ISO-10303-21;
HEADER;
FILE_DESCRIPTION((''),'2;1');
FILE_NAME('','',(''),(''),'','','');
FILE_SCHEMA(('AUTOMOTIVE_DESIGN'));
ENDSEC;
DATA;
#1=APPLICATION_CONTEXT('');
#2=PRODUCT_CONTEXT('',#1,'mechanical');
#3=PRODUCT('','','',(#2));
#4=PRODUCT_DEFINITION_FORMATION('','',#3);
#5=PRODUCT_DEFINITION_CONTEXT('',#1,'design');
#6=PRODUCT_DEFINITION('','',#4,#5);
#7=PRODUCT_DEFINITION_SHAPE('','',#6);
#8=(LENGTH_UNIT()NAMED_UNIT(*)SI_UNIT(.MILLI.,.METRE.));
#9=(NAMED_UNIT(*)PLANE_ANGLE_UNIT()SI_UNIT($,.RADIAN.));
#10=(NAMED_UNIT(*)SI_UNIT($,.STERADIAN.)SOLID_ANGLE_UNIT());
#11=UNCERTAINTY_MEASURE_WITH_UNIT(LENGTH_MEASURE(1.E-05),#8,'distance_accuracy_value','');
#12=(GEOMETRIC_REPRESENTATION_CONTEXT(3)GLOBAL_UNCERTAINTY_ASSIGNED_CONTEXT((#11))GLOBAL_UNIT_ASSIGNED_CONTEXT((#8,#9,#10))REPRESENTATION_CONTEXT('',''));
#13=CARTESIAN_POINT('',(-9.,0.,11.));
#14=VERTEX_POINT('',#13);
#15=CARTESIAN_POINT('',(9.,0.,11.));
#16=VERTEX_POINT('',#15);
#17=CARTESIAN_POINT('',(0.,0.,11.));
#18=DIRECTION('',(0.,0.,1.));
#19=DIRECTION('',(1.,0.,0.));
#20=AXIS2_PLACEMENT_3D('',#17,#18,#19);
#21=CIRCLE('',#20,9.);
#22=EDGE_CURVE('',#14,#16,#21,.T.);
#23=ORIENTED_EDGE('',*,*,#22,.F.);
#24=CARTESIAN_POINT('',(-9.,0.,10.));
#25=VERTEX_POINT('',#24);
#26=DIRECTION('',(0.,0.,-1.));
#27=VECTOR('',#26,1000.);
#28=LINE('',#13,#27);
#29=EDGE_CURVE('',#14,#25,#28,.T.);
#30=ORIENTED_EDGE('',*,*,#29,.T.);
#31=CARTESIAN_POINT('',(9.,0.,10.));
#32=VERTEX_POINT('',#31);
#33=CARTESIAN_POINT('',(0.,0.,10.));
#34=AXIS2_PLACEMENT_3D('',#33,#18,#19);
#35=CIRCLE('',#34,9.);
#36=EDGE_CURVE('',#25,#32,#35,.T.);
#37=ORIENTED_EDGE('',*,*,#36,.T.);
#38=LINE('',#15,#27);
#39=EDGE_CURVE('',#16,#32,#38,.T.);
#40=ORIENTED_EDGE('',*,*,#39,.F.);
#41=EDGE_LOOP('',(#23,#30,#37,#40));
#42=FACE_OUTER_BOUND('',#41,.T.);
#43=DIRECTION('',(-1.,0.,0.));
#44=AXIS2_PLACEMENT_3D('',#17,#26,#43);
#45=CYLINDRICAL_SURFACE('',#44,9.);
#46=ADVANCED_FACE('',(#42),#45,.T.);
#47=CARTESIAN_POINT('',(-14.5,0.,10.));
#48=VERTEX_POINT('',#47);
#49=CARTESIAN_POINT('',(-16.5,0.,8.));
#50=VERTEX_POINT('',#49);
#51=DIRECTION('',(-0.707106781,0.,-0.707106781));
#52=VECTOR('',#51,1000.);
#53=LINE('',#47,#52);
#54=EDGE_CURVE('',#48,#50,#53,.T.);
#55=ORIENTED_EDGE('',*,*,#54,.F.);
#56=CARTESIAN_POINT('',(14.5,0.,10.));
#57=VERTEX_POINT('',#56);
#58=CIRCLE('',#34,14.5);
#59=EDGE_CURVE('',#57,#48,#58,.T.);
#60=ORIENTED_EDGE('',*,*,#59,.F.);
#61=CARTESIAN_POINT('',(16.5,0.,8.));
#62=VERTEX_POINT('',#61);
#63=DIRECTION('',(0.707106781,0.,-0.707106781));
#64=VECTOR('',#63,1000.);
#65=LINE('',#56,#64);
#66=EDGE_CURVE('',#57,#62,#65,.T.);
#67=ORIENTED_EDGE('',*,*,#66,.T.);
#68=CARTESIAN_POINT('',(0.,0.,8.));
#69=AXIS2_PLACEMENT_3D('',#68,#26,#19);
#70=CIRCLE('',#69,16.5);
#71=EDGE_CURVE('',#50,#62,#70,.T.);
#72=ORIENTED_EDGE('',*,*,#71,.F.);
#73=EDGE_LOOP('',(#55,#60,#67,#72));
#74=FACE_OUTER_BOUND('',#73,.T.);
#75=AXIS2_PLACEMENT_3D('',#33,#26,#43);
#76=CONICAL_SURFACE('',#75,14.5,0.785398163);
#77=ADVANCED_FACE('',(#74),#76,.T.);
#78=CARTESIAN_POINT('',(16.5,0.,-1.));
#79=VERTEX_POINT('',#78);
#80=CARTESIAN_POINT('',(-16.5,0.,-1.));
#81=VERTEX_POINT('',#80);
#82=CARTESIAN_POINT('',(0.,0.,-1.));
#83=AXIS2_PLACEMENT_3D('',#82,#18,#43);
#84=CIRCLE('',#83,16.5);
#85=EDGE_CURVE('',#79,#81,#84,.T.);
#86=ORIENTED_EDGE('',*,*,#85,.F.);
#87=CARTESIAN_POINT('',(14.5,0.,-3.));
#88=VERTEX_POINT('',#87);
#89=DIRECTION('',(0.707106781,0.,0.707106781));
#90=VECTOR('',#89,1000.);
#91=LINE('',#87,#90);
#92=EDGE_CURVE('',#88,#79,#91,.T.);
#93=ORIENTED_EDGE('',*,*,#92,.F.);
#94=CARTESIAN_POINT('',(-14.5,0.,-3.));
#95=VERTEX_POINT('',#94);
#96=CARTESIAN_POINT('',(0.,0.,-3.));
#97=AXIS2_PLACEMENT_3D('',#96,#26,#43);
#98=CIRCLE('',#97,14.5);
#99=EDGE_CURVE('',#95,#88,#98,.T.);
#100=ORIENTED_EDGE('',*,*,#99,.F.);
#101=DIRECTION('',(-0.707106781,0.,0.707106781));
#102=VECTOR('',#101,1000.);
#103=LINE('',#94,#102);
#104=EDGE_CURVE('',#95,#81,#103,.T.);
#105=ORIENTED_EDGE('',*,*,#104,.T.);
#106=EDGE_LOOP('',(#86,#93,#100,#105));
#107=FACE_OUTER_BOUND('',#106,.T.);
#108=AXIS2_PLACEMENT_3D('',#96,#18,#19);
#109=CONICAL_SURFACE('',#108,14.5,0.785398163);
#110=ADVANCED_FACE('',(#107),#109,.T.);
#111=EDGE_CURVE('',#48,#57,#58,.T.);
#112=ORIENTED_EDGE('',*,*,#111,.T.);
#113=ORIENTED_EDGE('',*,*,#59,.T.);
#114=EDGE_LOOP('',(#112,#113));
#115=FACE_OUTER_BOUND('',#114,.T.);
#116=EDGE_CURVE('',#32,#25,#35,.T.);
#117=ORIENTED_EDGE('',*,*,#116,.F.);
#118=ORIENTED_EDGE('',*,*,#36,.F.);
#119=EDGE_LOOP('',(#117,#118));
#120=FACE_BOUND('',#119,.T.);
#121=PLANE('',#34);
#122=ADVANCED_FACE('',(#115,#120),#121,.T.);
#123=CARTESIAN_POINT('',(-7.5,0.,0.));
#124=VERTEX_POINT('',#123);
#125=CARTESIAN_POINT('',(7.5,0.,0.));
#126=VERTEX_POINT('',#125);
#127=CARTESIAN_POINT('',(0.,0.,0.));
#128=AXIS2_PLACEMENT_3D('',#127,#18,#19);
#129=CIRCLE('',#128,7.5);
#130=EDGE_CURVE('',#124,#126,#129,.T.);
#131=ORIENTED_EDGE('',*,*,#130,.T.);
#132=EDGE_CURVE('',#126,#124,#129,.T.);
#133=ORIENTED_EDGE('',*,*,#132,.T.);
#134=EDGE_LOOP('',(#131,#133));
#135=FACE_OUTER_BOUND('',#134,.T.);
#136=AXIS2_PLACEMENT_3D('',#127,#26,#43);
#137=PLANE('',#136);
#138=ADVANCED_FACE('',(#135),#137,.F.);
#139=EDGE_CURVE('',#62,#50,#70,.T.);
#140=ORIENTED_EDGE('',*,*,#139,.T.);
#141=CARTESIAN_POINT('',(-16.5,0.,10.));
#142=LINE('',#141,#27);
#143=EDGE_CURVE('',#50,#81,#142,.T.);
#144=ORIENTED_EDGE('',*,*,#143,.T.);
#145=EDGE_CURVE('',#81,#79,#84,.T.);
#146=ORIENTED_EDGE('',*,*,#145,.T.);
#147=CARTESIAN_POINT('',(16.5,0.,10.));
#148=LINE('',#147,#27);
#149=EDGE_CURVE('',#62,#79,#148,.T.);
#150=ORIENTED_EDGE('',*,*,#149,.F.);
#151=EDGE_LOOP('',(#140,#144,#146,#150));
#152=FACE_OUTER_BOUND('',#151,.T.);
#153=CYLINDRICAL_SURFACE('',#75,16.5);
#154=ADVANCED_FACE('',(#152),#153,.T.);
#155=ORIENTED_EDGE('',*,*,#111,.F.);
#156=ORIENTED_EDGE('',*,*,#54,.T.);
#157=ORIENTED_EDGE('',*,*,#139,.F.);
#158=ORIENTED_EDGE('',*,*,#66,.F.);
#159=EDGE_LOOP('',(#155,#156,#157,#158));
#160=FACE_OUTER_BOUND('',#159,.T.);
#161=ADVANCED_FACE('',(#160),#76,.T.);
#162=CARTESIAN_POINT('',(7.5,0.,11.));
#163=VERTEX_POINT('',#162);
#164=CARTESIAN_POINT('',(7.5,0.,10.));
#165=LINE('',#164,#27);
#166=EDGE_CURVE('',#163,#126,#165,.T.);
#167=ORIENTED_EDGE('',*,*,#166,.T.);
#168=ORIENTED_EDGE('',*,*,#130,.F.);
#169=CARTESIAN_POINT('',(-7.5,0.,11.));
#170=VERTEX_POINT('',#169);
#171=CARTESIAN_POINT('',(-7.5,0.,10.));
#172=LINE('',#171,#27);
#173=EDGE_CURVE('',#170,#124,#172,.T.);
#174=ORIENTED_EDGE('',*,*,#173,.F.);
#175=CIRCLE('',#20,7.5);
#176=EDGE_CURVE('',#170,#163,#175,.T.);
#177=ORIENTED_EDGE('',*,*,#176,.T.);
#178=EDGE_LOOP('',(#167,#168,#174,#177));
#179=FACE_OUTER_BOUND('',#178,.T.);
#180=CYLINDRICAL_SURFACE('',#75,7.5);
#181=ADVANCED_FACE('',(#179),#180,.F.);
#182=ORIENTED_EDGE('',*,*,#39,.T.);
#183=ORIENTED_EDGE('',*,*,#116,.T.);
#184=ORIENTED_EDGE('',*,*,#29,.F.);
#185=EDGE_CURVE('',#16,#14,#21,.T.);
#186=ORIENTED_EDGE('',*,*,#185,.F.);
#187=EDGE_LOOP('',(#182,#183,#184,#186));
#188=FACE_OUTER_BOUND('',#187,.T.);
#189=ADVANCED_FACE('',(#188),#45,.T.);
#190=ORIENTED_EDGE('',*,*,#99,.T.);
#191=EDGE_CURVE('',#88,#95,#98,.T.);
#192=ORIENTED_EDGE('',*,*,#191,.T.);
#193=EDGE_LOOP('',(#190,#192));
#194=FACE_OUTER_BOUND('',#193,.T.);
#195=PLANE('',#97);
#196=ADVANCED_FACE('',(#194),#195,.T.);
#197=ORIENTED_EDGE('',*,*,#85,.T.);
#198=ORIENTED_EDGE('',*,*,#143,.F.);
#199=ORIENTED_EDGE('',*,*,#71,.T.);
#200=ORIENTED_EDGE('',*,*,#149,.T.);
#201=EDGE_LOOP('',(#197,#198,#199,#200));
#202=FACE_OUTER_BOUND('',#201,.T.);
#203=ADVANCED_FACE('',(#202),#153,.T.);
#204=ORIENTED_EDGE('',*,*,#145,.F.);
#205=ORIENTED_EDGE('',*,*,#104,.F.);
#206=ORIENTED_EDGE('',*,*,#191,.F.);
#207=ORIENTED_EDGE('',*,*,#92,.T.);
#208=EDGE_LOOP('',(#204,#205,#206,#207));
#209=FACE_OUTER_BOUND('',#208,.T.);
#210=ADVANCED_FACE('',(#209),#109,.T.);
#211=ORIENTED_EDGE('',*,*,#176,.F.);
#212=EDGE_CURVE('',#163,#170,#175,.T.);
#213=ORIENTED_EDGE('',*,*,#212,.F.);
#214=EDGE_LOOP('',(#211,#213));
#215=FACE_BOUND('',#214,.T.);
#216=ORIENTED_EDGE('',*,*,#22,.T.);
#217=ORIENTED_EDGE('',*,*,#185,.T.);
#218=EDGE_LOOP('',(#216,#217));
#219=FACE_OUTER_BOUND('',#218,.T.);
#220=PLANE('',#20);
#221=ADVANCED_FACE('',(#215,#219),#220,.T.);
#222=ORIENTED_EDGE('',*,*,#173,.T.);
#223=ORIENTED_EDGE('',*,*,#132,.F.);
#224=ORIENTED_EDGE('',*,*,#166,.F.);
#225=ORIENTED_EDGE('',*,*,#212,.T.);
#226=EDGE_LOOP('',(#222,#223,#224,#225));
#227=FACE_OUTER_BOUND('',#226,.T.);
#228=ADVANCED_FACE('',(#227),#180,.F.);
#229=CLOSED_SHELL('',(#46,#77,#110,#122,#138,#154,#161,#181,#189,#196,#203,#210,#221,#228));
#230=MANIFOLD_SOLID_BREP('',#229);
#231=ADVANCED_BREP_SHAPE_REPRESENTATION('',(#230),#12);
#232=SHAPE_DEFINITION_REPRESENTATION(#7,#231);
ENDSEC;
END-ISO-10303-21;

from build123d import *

# Parameters (mm, degrees)
SKETCH_1_R      = 16.5
SKETCH_1_R_2    = 7.5
EXTRUDE_1_DEPTH = 10
SKETCH_2_R      = 9
SKETCH_2_R_2    = 7.5
EXTRUDE_2_DEPTH = 1
EXTRUDE_START   = 3
SKETCH_3_R      = 16.5
EXTRUDE_3_DEPTH = 3
CHAMFER_1_SIZE  = 2


with BuildPart() as part:
    # 草图1 → 凸台-拉伸1 (new body)
    with BuildSketch(Plane.XY):
        Circle(SKETCH_1_R)
        Circle(SKETCH_1_R_2, mode=Mode.SUBTRACT)
    extrude(amount=EXTRUDE_1_DEPTH)

    # 草图2 → 凸台-拉伸2 (add)
    with BuildSketch(Plane.XY.offset(10)):
        Circle(SKETCH_2_R)
        Circle(SKETCH_2_R_2, mode=Mode.SUBTRACT)
    extrude(amount=EXTRUDE_2_DEPTH)

    # 草图3 → 凸台-拉伸3 (add)
    with BuildSketch(Plane(origin=(0, 0, 0), x_dir=(-1, 0, 0), z_dir=(0, 0, -1)).offset(EXTRUDE_START)):
        Circle(SKETCH_3_R)
    extrude(amount=-EXTRUDE_3_DEPTH)

    # 倒角1
    chamfer_1_edges = [part.edges().sort_by_distance(p)[0] for p in [
        (16.5, 0, -3),
        (-16.5, 0, 10),
    ]]
    chamfer(chamfer_1_edges, length=CHAMFER_1_SIZE)


solid = part.part
